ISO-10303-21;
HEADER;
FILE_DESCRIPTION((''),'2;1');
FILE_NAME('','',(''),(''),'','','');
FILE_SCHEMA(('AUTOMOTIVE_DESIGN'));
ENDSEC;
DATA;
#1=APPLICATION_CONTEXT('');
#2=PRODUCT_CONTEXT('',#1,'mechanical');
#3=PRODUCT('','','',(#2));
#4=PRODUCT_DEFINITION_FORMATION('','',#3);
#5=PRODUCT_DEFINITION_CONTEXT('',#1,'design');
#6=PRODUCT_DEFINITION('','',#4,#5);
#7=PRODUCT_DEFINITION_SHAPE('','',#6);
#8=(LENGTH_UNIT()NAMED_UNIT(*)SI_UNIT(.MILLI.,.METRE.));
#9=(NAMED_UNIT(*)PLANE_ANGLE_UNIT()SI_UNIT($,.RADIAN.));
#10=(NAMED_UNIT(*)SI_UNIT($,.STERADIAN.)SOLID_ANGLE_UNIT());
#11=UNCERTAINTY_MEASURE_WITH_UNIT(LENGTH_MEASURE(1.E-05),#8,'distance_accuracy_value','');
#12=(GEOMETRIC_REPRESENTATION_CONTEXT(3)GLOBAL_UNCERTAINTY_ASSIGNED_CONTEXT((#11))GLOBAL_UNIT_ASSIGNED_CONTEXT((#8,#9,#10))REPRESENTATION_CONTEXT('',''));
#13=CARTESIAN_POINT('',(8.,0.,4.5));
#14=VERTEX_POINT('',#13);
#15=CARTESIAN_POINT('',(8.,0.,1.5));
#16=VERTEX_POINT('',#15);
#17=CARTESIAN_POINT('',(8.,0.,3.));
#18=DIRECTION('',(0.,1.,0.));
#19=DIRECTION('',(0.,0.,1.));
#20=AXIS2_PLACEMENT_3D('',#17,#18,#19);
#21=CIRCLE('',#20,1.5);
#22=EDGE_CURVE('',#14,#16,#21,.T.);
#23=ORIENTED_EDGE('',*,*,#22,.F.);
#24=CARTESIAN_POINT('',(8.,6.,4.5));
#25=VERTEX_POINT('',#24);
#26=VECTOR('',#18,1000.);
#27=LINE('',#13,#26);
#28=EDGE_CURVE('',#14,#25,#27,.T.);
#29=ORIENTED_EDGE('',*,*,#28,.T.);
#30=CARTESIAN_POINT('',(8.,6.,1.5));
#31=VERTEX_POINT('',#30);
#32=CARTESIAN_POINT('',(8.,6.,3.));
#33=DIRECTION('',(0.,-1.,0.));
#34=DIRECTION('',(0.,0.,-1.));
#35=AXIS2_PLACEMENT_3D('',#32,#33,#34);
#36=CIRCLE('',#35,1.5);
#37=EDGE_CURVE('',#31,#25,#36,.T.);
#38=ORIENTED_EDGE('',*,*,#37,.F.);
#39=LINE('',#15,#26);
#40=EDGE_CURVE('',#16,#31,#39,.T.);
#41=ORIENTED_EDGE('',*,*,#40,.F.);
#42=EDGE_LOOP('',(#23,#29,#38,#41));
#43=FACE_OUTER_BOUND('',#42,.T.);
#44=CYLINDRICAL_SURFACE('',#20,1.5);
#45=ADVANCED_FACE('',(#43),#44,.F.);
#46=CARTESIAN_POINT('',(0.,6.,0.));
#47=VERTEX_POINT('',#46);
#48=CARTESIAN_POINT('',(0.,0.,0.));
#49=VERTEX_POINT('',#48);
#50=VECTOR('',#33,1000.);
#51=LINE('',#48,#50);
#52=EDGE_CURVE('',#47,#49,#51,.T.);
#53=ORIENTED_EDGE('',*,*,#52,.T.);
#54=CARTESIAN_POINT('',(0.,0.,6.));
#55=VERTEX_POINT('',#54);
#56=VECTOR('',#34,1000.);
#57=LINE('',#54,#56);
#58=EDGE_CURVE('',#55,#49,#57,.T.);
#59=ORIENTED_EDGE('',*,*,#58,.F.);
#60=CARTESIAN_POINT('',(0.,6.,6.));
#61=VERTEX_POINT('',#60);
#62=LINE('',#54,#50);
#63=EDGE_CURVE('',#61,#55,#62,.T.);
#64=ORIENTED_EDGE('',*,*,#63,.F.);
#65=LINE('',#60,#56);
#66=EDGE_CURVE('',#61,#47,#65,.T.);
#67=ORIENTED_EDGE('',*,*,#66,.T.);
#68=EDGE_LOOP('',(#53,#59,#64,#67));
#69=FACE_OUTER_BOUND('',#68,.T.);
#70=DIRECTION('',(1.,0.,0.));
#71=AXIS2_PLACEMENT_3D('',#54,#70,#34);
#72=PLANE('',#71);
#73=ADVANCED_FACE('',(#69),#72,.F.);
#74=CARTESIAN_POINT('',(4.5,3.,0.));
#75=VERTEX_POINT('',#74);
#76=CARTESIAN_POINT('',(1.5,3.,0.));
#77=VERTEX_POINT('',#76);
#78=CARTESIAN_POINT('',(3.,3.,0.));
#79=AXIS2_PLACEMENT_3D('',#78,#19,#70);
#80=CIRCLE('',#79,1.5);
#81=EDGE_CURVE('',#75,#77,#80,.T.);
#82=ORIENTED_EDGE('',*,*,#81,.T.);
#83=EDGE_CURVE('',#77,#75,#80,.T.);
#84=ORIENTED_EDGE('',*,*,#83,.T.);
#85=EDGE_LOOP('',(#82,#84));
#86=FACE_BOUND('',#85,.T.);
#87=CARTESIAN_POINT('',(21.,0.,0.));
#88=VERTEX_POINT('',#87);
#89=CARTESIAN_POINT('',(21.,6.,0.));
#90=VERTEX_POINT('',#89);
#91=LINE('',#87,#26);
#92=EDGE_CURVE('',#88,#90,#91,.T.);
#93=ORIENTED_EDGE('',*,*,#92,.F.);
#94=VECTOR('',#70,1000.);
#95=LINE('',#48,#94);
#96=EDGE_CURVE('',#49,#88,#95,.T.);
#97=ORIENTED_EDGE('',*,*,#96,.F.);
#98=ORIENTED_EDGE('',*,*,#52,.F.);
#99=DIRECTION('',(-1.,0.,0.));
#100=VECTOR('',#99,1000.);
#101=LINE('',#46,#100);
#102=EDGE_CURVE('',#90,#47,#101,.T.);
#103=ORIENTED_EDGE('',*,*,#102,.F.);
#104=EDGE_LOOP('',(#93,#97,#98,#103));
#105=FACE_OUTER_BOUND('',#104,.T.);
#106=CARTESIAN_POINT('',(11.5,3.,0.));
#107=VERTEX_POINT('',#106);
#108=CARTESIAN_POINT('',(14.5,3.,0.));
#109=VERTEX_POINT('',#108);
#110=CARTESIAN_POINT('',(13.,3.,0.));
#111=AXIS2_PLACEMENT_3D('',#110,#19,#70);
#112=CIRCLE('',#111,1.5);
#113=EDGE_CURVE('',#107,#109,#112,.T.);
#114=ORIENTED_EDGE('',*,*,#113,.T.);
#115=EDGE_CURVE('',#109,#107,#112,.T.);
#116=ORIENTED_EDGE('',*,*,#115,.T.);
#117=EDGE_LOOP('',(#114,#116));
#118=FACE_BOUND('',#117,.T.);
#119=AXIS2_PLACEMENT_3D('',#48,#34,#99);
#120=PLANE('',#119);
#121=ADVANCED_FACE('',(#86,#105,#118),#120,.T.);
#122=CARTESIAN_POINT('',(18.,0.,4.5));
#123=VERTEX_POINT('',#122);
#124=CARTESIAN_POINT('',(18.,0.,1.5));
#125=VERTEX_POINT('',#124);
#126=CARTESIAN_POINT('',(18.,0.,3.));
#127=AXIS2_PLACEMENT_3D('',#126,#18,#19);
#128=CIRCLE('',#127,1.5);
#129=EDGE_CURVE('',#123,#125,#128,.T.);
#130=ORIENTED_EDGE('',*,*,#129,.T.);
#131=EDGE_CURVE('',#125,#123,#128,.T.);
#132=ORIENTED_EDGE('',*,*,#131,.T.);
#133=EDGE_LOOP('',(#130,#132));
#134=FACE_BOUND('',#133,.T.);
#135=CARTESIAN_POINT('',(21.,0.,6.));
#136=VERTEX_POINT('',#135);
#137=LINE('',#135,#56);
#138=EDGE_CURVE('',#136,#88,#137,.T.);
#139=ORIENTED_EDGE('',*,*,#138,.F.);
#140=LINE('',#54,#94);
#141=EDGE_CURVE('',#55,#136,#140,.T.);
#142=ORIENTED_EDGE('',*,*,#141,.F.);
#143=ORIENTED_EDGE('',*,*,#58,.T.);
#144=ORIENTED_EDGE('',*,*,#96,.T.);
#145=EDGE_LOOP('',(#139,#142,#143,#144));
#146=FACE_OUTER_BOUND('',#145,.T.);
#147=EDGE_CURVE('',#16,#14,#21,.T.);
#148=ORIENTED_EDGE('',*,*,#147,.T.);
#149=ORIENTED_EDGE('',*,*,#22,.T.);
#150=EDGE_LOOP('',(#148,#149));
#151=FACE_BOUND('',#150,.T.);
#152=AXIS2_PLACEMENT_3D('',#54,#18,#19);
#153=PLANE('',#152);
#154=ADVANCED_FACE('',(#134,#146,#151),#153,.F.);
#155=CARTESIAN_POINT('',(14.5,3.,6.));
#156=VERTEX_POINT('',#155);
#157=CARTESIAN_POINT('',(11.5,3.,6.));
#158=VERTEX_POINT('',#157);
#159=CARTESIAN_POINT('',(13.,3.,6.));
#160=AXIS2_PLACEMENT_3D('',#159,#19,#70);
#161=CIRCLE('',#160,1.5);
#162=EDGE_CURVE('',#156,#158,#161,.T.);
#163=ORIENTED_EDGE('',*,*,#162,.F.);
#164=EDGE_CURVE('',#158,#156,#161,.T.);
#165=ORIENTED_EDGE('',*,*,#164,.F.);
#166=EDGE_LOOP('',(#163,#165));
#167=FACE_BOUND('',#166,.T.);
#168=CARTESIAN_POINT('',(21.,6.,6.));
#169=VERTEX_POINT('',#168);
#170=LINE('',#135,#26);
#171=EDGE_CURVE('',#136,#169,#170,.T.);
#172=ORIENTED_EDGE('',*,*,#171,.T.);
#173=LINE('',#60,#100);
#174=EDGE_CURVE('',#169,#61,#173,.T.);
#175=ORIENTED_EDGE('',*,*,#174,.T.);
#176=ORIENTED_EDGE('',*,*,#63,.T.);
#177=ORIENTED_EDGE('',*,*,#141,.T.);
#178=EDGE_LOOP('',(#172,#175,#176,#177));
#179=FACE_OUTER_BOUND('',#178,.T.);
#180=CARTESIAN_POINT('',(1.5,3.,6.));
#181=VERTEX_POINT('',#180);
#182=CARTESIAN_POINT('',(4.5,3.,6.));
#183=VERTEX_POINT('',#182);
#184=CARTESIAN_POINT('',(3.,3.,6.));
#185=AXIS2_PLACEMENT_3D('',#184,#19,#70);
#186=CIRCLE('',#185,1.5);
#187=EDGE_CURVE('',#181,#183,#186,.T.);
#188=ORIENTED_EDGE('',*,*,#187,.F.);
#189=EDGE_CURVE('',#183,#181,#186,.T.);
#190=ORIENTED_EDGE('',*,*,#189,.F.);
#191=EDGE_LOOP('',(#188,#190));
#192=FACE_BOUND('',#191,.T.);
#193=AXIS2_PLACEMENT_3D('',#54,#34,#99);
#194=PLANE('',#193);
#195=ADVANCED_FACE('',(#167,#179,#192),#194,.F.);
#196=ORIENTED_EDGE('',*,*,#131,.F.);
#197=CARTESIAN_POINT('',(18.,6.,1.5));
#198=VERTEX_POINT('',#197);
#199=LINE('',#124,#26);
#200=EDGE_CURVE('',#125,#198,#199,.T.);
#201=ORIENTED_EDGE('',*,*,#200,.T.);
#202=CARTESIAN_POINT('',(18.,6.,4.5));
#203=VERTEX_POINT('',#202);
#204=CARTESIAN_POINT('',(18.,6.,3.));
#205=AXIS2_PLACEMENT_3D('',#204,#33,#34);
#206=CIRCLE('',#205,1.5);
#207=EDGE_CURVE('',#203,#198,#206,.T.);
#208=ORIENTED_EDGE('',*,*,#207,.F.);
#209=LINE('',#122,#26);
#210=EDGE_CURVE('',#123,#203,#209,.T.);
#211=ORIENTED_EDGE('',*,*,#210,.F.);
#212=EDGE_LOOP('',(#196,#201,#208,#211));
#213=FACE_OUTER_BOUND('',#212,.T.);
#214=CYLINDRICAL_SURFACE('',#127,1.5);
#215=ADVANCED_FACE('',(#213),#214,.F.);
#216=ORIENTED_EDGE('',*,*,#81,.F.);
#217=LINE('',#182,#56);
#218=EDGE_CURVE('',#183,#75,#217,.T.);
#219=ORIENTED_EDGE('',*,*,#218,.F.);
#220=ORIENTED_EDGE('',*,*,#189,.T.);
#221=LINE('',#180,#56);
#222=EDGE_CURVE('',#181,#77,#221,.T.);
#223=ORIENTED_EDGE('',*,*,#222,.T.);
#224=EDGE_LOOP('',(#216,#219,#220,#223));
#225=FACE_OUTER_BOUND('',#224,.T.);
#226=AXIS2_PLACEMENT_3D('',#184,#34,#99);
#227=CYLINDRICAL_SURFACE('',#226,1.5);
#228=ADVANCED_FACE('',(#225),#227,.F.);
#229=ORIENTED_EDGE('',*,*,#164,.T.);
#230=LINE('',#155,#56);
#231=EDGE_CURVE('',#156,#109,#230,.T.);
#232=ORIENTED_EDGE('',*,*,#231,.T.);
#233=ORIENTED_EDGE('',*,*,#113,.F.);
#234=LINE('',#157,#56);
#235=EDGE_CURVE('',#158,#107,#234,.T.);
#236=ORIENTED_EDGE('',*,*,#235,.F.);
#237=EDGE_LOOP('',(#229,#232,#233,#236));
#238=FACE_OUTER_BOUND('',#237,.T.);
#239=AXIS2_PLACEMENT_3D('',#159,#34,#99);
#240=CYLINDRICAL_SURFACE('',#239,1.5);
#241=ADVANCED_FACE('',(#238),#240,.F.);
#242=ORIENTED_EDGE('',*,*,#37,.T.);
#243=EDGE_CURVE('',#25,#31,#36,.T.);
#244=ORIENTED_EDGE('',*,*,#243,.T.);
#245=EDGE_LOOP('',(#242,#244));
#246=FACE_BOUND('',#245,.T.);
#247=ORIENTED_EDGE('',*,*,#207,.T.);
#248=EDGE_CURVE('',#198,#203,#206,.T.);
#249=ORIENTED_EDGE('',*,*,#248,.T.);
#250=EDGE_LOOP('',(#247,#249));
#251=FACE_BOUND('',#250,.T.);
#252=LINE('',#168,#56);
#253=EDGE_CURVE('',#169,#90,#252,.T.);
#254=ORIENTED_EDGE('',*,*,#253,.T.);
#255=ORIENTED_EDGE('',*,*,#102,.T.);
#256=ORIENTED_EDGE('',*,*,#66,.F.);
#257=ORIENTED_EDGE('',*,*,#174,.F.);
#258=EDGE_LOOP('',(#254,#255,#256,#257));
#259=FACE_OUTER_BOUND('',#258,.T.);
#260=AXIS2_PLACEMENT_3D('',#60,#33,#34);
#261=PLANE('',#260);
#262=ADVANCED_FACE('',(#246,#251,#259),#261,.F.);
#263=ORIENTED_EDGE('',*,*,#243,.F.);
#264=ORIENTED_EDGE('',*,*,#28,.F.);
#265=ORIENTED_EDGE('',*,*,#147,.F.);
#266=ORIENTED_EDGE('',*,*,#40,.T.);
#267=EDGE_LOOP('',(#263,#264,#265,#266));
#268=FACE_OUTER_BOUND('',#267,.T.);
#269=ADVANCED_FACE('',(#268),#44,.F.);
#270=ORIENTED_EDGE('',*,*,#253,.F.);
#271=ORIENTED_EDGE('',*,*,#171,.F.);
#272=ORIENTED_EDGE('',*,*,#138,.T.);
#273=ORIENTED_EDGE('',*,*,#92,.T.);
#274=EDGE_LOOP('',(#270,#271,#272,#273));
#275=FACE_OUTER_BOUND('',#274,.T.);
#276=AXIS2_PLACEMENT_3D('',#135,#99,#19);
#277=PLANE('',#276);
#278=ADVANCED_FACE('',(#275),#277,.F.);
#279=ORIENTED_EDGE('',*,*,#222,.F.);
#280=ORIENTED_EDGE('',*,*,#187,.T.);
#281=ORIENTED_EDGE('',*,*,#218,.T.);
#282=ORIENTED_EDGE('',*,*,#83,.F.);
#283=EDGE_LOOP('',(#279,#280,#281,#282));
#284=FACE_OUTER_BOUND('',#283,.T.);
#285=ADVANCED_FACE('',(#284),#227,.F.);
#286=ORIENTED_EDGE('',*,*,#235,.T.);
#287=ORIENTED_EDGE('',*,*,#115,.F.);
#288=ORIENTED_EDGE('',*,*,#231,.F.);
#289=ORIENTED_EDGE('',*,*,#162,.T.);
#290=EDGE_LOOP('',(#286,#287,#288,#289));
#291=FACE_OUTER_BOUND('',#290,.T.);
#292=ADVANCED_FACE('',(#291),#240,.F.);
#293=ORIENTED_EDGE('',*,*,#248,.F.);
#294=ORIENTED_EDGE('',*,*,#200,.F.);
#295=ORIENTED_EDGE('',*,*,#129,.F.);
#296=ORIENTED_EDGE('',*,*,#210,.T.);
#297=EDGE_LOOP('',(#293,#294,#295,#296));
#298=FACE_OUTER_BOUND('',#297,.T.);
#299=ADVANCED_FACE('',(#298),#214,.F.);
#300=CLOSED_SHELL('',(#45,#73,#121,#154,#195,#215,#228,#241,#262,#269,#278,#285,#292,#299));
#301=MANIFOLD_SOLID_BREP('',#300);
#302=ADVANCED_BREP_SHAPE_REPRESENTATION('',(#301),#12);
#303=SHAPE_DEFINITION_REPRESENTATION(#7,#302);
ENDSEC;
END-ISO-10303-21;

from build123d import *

# Parameters (mm, degrees)
SKETCH_1_W               = 21
SKETCH_1_H               = 6
SKETCH_1_R               = 1.5
EXTRUDE_1_DEPTH          = 6
CUT_EXTRUDE_1_DEPTH      = 23.649503306
CUT_EXTRUDE_1_DEPTH_BACK = 23.649503306
SKETCH_2_R               = 1.5


with BuildPart() as part:
    # 草图1 → 凸台-拉伸1 (new body)
    with BuildSketch(Plane.XY):
        with Locations((10.5, 3)):
            Rectangle(SKETCH_1_W, SKETCH_1_H)
        with Locations((3, 3)):
            Circle(SKETCH_1_R, mode=Mode.SUBTRACT)
        with Locations((13, 3)):
            Circle(SKETCH_1_R, mode=Mode.SUBTRACT)
    extrude(amount=EXTRUDE_1_DEPTH)

    # 草图2 → 切除-拉伸1 (cut, two sides: drawn at the far end of the back side and taken through both)
    with BuildSketch(Plane(origin=(0, 6, 0), x_dir=(1, 0, 0), z_dir=(0, 1, 0)).offset(-CUT_EXTRUDE_1_DEPTH_BACK)):
        with Locations(Location((8, -3, 0), (0, 0, 270))):
            Circle(SKETCH_2_R)
        with Locations(Location((18, -3, 0), (0, 0, 270))):
            Circle(SKETCH_2_R)
    extrude(amount=CUT_EXTRUDE_1_DEPTH + CUT_EXTRUDE_1_DEPTH_BACK, mode=Mode.SUBTRACT)


solid = part.part
